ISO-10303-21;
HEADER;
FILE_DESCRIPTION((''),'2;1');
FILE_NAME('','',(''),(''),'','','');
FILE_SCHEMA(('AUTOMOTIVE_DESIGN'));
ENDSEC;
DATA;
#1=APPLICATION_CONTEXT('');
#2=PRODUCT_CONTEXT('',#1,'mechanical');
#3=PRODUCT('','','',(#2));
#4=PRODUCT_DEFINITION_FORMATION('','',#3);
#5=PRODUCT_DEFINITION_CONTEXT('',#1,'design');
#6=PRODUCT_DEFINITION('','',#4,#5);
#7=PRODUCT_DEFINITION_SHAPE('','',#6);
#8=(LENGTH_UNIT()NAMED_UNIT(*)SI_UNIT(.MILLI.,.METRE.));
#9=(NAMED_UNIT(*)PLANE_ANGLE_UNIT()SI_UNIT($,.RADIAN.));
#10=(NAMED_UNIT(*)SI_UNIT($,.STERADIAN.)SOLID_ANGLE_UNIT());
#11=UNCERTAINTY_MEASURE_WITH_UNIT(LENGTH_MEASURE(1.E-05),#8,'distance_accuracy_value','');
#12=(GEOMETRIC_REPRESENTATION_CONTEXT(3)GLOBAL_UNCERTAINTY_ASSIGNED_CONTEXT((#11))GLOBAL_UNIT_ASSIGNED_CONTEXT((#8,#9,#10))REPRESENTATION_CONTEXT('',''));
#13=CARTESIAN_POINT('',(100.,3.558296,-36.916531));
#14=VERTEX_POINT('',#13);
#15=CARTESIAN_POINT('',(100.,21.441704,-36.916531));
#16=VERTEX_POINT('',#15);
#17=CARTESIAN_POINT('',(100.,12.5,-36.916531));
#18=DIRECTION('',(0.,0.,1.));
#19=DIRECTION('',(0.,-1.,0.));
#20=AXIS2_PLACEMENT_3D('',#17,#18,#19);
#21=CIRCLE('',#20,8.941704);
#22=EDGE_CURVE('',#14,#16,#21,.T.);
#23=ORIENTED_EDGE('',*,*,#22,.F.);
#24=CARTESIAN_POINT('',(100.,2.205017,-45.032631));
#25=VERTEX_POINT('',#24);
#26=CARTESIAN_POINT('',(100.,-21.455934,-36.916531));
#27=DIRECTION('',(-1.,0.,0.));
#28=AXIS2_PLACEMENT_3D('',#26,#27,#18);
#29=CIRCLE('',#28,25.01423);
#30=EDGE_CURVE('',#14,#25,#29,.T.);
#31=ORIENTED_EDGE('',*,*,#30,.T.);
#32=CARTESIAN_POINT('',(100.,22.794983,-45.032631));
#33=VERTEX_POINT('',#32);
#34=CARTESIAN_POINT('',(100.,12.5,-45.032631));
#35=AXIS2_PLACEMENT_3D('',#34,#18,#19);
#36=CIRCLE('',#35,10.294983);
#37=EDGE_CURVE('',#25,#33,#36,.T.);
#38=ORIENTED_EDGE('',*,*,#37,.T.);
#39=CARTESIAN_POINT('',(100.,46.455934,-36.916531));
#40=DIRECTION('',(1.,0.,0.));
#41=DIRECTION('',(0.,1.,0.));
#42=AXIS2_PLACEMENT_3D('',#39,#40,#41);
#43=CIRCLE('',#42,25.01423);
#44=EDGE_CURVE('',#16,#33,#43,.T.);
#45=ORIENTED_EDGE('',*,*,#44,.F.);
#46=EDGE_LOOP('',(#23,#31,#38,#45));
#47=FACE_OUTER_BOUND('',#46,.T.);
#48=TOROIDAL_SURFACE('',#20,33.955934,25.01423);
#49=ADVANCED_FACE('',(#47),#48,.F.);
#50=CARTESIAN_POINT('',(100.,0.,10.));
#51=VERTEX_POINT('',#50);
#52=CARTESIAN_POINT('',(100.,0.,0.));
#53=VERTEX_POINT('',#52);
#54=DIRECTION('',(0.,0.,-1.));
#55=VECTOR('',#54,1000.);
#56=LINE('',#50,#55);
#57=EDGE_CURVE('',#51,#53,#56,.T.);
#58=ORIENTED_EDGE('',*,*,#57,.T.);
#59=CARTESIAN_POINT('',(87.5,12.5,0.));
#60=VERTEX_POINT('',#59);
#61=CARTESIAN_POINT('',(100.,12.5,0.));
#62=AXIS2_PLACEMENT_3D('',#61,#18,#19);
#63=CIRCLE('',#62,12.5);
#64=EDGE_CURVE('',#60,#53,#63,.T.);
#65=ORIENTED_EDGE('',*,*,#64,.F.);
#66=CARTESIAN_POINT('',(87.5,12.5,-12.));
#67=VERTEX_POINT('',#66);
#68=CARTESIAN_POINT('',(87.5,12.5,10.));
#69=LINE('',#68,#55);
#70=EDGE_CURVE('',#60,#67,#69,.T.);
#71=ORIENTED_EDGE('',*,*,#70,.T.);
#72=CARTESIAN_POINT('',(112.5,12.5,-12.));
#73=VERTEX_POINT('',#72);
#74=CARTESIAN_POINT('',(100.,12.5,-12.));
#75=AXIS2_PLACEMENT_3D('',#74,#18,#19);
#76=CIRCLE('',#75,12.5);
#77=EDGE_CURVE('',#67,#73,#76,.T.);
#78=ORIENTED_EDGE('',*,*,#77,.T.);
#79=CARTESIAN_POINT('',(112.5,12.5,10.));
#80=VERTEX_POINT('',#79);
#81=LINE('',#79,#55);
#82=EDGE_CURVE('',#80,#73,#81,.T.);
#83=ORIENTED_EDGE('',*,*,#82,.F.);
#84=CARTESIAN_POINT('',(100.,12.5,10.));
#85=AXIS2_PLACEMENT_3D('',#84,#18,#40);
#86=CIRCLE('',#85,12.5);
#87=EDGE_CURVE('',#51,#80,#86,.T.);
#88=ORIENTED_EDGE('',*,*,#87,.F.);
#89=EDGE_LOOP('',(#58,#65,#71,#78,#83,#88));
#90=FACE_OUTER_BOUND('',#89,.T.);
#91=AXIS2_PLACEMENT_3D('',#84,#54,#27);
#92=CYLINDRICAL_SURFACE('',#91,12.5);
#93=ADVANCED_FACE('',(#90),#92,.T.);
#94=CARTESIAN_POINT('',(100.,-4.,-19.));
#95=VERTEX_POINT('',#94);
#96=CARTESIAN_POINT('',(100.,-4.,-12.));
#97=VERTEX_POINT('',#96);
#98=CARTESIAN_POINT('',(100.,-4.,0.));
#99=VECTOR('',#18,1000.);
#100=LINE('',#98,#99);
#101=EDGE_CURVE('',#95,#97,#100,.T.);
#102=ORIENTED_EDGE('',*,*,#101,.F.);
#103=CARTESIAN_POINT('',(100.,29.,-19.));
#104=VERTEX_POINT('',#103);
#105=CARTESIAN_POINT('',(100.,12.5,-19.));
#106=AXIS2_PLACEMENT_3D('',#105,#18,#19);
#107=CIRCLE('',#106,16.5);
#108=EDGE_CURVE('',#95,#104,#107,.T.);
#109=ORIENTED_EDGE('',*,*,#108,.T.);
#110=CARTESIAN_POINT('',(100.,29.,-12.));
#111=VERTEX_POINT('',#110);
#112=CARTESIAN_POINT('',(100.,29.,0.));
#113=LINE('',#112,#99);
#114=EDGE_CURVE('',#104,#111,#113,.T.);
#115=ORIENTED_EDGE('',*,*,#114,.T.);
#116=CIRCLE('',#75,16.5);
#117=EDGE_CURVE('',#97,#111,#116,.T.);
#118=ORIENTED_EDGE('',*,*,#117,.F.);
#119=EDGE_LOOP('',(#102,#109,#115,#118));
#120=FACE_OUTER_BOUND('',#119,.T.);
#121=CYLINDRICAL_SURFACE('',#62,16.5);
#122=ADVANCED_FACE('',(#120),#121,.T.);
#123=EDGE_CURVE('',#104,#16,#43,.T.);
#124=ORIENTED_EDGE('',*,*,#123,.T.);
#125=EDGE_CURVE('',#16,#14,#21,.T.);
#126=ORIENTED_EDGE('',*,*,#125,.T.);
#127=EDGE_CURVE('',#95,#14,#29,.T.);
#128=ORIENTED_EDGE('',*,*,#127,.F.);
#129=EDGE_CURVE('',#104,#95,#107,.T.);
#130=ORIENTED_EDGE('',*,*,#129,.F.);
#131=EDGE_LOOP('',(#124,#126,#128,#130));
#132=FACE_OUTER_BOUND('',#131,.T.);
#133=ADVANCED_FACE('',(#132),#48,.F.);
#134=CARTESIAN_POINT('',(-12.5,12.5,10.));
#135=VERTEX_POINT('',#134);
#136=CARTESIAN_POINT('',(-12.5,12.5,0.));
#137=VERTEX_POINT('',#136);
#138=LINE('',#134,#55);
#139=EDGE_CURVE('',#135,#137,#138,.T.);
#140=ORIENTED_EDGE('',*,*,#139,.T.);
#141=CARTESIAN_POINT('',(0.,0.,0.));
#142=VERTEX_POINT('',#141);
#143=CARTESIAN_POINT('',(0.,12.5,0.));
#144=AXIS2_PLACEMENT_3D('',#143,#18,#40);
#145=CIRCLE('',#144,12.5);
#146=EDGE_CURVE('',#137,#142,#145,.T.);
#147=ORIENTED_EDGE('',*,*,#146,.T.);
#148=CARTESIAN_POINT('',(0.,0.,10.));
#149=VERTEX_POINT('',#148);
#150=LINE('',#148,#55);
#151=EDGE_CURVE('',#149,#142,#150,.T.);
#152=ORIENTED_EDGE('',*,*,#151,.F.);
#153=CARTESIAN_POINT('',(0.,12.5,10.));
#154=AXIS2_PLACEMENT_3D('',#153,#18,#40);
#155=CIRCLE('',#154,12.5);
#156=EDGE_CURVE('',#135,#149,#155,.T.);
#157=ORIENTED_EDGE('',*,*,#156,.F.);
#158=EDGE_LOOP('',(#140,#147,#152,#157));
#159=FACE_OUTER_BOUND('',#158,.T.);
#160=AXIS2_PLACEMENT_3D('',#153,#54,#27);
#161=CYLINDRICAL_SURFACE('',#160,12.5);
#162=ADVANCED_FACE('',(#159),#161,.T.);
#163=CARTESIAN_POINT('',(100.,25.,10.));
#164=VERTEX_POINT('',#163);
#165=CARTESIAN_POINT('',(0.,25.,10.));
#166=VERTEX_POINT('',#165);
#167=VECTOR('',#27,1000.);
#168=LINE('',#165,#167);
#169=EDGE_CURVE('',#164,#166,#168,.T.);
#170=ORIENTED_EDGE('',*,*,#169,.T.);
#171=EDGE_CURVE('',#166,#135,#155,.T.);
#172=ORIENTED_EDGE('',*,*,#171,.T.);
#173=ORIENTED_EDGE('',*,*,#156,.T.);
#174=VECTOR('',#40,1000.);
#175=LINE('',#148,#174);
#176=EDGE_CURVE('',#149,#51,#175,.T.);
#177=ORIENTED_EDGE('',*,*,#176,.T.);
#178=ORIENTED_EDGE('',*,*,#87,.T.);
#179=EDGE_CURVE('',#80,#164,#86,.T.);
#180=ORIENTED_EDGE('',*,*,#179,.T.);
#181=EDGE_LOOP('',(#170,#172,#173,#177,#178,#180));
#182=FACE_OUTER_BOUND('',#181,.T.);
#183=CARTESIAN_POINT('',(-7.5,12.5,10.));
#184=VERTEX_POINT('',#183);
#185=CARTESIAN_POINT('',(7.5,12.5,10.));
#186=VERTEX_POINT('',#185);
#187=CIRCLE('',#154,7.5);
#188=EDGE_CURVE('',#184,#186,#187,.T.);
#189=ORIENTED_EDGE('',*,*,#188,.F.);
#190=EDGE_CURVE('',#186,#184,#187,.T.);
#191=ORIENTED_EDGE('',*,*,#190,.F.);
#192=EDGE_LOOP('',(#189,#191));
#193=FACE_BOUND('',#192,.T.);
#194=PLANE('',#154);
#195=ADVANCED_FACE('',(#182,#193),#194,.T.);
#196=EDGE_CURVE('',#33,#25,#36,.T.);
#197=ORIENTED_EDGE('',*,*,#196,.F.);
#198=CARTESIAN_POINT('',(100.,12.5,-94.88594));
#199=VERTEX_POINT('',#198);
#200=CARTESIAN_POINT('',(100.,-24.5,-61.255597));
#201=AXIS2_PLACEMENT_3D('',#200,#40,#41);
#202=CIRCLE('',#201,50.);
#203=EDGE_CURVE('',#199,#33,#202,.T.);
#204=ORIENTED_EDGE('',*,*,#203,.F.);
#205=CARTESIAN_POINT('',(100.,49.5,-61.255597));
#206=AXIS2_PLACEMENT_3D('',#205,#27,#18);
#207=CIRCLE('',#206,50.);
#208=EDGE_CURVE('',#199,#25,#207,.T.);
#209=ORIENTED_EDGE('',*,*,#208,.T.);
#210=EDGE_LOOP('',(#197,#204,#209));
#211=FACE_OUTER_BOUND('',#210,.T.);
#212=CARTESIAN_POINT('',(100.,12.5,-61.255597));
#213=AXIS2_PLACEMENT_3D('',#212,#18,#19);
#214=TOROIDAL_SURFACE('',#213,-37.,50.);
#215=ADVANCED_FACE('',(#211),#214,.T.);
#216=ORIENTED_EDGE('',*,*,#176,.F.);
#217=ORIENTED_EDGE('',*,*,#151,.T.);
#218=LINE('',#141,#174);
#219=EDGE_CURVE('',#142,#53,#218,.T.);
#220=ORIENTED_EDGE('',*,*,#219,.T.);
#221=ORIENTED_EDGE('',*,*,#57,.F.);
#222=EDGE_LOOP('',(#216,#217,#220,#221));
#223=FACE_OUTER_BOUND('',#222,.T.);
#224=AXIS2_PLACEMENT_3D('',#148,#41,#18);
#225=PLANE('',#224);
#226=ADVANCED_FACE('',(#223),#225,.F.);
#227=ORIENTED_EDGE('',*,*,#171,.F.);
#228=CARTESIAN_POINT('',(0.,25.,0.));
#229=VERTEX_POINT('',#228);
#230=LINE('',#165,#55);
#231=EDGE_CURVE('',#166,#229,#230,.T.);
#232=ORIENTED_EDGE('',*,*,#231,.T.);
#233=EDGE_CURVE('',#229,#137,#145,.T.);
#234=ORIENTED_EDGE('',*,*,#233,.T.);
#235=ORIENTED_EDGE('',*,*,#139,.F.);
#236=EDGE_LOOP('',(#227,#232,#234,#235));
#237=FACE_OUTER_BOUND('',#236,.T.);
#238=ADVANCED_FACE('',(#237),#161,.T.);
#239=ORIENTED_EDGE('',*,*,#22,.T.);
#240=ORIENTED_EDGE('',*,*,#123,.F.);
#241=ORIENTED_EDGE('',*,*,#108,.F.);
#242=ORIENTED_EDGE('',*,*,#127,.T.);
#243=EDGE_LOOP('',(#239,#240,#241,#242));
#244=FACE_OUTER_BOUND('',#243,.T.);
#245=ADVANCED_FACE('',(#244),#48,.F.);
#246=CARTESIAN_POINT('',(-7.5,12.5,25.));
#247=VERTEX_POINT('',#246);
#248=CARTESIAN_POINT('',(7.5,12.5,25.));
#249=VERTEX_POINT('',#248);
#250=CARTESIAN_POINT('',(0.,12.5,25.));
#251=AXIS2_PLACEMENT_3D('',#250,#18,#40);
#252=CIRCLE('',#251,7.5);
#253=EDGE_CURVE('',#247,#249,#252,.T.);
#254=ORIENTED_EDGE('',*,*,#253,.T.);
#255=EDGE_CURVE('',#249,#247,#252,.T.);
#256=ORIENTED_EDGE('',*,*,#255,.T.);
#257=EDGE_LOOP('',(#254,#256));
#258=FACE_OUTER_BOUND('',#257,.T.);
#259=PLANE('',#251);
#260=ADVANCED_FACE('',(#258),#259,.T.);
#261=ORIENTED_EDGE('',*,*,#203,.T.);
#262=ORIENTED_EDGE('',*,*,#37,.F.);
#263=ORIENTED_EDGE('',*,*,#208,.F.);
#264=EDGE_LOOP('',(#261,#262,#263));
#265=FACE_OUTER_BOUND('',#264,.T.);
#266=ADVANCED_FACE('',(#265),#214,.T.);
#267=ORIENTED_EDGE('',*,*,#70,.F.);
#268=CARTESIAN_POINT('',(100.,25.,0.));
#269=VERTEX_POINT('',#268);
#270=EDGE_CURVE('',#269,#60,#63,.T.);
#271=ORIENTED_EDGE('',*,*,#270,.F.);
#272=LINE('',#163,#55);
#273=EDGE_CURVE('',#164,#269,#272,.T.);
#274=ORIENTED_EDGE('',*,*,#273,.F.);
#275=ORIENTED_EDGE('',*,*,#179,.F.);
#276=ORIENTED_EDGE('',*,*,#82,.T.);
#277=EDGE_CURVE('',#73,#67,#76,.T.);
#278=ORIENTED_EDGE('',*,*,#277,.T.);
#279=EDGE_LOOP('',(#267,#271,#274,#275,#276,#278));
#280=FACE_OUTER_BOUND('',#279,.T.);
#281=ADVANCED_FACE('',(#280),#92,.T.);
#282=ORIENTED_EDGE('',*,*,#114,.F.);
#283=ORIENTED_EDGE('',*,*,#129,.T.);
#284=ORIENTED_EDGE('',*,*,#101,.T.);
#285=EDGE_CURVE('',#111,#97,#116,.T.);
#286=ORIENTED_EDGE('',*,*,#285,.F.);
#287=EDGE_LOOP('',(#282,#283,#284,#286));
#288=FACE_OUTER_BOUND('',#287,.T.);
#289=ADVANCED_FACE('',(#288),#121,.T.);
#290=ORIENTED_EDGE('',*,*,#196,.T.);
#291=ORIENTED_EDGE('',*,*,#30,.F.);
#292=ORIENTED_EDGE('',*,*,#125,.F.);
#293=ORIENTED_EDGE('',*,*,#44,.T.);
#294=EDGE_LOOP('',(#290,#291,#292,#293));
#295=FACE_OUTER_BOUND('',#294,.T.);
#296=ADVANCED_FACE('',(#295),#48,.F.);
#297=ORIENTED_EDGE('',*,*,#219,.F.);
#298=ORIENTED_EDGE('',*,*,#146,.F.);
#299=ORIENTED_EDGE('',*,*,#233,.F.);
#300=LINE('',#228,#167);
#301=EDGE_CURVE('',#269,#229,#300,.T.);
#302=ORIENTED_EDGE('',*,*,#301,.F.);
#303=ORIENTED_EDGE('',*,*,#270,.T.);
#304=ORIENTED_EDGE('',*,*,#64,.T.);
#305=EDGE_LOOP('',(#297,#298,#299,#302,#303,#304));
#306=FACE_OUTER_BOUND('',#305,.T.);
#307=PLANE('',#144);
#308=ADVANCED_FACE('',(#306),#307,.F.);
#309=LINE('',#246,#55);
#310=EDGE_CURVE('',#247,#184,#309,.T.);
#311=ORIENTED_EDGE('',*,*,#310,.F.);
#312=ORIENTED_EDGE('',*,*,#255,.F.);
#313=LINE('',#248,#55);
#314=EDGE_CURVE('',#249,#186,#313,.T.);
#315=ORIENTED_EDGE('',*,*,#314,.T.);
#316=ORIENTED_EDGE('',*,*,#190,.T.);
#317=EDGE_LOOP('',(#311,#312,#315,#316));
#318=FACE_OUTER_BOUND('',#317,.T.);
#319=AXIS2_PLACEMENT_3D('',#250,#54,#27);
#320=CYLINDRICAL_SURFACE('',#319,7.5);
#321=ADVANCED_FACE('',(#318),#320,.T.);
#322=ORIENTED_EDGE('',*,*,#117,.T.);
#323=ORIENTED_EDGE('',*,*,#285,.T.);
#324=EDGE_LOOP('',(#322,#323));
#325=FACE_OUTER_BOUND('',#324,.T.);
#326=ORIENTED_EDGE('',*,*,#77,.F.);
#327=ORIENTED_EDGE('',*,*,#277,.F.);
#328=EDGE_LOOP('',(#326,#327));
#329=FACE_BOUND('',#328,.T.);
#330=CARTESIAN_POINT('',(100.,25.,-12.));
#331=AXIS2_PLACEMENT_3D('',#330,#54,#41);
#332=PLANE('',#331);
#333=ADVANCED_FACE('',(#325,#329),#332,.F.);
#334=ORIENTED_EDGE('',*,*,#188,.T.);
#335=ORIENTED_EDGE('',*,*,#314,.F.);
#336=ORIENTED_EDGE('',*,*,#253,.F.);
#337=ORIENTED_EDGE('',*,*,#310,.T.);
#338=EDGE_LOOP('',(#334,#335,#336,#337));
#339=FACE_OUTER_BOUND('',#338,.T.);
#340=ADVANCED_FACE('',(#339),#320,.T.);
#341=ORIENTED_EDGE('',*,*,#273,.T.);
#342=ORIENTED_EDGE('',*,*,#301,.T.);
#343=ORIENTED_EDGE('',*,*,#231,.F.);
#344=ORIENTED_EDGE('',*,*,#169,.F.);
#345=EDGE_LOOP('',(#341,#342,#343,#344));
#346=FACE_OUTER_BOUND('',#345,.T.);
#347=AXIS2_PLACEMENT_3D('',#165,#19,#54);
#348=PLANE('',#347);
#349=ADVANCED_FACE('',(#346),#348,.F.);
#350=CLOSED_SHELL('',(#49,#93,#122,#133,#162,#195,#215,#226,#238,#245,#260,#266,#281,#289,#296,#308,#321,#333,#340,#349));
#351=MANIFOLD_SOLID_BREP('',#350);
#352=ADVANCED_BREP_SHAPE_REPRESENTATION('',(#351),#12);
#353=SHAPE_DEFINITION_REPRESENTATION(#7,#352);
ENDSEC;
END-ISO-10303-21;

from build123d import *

# Parameters (mm, degrees)
EXTRUDE_1_DEPTH = 10
SKETCH_2_R      = 7.5
EXTRUDE_2_DEPTH = 15


with BuildPart() as part:
    # 草图1 → 凸台-拉伸1 (new body)
    with BuildSketch(Plane.XY):
        with BuildLine():
            Line((0, 0), (100, 0))
            ThreePointArc((100, 0), (112.5, 12.5), (100, 25))
            Line((100, 25), (0, 25))
            ThreePointArc((0, 25), (-12.5, 12.5), (0, 0))
        make_face()
    extrude(amount=EXTRUDE_1_DEPTH)

    # 草图2 → 凸台-拉伸2 (add)
    with BuildSketch(Plane.XY.offset(10)):
        with Locations((0, 12.5)):
            Circle(SKETCH_2_R)
    extrude(amount=EXTRUDE_2_DEPTH)

    # 草图7 → 旋转1 (revolve)
    with BuildSketch(Plane(origin=(100, 0, 0), x_dir=(0, 0, -1), z_dir=(1, 0, 0)), mode=Mode.PRIVATE) as revolve_1_sk:
        with BuildLine():
            Line((0, 12.5), (0, 25))
            Line((0, 25), (12, 25))
            Line((12, 25), (12, 29))
            Line((12, 29), (19, 29))
            ThreePointArc((19, 29), (31.116731463, 22.12336259), (45.032630645, 22.794982573))
            ThreePointArc((45.032630645, 22.794982573), (71.367513527, 24.466816677), (94.885940011, 12.5))
            Line((94.885940011, 12.5), (0, 12.5))
        make_face()
    revolve(revolve_1_sk.sketch.rotate(Axis((100, 12.5, 0), (0, 0, -1)), 180), axis=Axis((100, 12.5, 0), (0, 0, -1)))


solid = part.part
